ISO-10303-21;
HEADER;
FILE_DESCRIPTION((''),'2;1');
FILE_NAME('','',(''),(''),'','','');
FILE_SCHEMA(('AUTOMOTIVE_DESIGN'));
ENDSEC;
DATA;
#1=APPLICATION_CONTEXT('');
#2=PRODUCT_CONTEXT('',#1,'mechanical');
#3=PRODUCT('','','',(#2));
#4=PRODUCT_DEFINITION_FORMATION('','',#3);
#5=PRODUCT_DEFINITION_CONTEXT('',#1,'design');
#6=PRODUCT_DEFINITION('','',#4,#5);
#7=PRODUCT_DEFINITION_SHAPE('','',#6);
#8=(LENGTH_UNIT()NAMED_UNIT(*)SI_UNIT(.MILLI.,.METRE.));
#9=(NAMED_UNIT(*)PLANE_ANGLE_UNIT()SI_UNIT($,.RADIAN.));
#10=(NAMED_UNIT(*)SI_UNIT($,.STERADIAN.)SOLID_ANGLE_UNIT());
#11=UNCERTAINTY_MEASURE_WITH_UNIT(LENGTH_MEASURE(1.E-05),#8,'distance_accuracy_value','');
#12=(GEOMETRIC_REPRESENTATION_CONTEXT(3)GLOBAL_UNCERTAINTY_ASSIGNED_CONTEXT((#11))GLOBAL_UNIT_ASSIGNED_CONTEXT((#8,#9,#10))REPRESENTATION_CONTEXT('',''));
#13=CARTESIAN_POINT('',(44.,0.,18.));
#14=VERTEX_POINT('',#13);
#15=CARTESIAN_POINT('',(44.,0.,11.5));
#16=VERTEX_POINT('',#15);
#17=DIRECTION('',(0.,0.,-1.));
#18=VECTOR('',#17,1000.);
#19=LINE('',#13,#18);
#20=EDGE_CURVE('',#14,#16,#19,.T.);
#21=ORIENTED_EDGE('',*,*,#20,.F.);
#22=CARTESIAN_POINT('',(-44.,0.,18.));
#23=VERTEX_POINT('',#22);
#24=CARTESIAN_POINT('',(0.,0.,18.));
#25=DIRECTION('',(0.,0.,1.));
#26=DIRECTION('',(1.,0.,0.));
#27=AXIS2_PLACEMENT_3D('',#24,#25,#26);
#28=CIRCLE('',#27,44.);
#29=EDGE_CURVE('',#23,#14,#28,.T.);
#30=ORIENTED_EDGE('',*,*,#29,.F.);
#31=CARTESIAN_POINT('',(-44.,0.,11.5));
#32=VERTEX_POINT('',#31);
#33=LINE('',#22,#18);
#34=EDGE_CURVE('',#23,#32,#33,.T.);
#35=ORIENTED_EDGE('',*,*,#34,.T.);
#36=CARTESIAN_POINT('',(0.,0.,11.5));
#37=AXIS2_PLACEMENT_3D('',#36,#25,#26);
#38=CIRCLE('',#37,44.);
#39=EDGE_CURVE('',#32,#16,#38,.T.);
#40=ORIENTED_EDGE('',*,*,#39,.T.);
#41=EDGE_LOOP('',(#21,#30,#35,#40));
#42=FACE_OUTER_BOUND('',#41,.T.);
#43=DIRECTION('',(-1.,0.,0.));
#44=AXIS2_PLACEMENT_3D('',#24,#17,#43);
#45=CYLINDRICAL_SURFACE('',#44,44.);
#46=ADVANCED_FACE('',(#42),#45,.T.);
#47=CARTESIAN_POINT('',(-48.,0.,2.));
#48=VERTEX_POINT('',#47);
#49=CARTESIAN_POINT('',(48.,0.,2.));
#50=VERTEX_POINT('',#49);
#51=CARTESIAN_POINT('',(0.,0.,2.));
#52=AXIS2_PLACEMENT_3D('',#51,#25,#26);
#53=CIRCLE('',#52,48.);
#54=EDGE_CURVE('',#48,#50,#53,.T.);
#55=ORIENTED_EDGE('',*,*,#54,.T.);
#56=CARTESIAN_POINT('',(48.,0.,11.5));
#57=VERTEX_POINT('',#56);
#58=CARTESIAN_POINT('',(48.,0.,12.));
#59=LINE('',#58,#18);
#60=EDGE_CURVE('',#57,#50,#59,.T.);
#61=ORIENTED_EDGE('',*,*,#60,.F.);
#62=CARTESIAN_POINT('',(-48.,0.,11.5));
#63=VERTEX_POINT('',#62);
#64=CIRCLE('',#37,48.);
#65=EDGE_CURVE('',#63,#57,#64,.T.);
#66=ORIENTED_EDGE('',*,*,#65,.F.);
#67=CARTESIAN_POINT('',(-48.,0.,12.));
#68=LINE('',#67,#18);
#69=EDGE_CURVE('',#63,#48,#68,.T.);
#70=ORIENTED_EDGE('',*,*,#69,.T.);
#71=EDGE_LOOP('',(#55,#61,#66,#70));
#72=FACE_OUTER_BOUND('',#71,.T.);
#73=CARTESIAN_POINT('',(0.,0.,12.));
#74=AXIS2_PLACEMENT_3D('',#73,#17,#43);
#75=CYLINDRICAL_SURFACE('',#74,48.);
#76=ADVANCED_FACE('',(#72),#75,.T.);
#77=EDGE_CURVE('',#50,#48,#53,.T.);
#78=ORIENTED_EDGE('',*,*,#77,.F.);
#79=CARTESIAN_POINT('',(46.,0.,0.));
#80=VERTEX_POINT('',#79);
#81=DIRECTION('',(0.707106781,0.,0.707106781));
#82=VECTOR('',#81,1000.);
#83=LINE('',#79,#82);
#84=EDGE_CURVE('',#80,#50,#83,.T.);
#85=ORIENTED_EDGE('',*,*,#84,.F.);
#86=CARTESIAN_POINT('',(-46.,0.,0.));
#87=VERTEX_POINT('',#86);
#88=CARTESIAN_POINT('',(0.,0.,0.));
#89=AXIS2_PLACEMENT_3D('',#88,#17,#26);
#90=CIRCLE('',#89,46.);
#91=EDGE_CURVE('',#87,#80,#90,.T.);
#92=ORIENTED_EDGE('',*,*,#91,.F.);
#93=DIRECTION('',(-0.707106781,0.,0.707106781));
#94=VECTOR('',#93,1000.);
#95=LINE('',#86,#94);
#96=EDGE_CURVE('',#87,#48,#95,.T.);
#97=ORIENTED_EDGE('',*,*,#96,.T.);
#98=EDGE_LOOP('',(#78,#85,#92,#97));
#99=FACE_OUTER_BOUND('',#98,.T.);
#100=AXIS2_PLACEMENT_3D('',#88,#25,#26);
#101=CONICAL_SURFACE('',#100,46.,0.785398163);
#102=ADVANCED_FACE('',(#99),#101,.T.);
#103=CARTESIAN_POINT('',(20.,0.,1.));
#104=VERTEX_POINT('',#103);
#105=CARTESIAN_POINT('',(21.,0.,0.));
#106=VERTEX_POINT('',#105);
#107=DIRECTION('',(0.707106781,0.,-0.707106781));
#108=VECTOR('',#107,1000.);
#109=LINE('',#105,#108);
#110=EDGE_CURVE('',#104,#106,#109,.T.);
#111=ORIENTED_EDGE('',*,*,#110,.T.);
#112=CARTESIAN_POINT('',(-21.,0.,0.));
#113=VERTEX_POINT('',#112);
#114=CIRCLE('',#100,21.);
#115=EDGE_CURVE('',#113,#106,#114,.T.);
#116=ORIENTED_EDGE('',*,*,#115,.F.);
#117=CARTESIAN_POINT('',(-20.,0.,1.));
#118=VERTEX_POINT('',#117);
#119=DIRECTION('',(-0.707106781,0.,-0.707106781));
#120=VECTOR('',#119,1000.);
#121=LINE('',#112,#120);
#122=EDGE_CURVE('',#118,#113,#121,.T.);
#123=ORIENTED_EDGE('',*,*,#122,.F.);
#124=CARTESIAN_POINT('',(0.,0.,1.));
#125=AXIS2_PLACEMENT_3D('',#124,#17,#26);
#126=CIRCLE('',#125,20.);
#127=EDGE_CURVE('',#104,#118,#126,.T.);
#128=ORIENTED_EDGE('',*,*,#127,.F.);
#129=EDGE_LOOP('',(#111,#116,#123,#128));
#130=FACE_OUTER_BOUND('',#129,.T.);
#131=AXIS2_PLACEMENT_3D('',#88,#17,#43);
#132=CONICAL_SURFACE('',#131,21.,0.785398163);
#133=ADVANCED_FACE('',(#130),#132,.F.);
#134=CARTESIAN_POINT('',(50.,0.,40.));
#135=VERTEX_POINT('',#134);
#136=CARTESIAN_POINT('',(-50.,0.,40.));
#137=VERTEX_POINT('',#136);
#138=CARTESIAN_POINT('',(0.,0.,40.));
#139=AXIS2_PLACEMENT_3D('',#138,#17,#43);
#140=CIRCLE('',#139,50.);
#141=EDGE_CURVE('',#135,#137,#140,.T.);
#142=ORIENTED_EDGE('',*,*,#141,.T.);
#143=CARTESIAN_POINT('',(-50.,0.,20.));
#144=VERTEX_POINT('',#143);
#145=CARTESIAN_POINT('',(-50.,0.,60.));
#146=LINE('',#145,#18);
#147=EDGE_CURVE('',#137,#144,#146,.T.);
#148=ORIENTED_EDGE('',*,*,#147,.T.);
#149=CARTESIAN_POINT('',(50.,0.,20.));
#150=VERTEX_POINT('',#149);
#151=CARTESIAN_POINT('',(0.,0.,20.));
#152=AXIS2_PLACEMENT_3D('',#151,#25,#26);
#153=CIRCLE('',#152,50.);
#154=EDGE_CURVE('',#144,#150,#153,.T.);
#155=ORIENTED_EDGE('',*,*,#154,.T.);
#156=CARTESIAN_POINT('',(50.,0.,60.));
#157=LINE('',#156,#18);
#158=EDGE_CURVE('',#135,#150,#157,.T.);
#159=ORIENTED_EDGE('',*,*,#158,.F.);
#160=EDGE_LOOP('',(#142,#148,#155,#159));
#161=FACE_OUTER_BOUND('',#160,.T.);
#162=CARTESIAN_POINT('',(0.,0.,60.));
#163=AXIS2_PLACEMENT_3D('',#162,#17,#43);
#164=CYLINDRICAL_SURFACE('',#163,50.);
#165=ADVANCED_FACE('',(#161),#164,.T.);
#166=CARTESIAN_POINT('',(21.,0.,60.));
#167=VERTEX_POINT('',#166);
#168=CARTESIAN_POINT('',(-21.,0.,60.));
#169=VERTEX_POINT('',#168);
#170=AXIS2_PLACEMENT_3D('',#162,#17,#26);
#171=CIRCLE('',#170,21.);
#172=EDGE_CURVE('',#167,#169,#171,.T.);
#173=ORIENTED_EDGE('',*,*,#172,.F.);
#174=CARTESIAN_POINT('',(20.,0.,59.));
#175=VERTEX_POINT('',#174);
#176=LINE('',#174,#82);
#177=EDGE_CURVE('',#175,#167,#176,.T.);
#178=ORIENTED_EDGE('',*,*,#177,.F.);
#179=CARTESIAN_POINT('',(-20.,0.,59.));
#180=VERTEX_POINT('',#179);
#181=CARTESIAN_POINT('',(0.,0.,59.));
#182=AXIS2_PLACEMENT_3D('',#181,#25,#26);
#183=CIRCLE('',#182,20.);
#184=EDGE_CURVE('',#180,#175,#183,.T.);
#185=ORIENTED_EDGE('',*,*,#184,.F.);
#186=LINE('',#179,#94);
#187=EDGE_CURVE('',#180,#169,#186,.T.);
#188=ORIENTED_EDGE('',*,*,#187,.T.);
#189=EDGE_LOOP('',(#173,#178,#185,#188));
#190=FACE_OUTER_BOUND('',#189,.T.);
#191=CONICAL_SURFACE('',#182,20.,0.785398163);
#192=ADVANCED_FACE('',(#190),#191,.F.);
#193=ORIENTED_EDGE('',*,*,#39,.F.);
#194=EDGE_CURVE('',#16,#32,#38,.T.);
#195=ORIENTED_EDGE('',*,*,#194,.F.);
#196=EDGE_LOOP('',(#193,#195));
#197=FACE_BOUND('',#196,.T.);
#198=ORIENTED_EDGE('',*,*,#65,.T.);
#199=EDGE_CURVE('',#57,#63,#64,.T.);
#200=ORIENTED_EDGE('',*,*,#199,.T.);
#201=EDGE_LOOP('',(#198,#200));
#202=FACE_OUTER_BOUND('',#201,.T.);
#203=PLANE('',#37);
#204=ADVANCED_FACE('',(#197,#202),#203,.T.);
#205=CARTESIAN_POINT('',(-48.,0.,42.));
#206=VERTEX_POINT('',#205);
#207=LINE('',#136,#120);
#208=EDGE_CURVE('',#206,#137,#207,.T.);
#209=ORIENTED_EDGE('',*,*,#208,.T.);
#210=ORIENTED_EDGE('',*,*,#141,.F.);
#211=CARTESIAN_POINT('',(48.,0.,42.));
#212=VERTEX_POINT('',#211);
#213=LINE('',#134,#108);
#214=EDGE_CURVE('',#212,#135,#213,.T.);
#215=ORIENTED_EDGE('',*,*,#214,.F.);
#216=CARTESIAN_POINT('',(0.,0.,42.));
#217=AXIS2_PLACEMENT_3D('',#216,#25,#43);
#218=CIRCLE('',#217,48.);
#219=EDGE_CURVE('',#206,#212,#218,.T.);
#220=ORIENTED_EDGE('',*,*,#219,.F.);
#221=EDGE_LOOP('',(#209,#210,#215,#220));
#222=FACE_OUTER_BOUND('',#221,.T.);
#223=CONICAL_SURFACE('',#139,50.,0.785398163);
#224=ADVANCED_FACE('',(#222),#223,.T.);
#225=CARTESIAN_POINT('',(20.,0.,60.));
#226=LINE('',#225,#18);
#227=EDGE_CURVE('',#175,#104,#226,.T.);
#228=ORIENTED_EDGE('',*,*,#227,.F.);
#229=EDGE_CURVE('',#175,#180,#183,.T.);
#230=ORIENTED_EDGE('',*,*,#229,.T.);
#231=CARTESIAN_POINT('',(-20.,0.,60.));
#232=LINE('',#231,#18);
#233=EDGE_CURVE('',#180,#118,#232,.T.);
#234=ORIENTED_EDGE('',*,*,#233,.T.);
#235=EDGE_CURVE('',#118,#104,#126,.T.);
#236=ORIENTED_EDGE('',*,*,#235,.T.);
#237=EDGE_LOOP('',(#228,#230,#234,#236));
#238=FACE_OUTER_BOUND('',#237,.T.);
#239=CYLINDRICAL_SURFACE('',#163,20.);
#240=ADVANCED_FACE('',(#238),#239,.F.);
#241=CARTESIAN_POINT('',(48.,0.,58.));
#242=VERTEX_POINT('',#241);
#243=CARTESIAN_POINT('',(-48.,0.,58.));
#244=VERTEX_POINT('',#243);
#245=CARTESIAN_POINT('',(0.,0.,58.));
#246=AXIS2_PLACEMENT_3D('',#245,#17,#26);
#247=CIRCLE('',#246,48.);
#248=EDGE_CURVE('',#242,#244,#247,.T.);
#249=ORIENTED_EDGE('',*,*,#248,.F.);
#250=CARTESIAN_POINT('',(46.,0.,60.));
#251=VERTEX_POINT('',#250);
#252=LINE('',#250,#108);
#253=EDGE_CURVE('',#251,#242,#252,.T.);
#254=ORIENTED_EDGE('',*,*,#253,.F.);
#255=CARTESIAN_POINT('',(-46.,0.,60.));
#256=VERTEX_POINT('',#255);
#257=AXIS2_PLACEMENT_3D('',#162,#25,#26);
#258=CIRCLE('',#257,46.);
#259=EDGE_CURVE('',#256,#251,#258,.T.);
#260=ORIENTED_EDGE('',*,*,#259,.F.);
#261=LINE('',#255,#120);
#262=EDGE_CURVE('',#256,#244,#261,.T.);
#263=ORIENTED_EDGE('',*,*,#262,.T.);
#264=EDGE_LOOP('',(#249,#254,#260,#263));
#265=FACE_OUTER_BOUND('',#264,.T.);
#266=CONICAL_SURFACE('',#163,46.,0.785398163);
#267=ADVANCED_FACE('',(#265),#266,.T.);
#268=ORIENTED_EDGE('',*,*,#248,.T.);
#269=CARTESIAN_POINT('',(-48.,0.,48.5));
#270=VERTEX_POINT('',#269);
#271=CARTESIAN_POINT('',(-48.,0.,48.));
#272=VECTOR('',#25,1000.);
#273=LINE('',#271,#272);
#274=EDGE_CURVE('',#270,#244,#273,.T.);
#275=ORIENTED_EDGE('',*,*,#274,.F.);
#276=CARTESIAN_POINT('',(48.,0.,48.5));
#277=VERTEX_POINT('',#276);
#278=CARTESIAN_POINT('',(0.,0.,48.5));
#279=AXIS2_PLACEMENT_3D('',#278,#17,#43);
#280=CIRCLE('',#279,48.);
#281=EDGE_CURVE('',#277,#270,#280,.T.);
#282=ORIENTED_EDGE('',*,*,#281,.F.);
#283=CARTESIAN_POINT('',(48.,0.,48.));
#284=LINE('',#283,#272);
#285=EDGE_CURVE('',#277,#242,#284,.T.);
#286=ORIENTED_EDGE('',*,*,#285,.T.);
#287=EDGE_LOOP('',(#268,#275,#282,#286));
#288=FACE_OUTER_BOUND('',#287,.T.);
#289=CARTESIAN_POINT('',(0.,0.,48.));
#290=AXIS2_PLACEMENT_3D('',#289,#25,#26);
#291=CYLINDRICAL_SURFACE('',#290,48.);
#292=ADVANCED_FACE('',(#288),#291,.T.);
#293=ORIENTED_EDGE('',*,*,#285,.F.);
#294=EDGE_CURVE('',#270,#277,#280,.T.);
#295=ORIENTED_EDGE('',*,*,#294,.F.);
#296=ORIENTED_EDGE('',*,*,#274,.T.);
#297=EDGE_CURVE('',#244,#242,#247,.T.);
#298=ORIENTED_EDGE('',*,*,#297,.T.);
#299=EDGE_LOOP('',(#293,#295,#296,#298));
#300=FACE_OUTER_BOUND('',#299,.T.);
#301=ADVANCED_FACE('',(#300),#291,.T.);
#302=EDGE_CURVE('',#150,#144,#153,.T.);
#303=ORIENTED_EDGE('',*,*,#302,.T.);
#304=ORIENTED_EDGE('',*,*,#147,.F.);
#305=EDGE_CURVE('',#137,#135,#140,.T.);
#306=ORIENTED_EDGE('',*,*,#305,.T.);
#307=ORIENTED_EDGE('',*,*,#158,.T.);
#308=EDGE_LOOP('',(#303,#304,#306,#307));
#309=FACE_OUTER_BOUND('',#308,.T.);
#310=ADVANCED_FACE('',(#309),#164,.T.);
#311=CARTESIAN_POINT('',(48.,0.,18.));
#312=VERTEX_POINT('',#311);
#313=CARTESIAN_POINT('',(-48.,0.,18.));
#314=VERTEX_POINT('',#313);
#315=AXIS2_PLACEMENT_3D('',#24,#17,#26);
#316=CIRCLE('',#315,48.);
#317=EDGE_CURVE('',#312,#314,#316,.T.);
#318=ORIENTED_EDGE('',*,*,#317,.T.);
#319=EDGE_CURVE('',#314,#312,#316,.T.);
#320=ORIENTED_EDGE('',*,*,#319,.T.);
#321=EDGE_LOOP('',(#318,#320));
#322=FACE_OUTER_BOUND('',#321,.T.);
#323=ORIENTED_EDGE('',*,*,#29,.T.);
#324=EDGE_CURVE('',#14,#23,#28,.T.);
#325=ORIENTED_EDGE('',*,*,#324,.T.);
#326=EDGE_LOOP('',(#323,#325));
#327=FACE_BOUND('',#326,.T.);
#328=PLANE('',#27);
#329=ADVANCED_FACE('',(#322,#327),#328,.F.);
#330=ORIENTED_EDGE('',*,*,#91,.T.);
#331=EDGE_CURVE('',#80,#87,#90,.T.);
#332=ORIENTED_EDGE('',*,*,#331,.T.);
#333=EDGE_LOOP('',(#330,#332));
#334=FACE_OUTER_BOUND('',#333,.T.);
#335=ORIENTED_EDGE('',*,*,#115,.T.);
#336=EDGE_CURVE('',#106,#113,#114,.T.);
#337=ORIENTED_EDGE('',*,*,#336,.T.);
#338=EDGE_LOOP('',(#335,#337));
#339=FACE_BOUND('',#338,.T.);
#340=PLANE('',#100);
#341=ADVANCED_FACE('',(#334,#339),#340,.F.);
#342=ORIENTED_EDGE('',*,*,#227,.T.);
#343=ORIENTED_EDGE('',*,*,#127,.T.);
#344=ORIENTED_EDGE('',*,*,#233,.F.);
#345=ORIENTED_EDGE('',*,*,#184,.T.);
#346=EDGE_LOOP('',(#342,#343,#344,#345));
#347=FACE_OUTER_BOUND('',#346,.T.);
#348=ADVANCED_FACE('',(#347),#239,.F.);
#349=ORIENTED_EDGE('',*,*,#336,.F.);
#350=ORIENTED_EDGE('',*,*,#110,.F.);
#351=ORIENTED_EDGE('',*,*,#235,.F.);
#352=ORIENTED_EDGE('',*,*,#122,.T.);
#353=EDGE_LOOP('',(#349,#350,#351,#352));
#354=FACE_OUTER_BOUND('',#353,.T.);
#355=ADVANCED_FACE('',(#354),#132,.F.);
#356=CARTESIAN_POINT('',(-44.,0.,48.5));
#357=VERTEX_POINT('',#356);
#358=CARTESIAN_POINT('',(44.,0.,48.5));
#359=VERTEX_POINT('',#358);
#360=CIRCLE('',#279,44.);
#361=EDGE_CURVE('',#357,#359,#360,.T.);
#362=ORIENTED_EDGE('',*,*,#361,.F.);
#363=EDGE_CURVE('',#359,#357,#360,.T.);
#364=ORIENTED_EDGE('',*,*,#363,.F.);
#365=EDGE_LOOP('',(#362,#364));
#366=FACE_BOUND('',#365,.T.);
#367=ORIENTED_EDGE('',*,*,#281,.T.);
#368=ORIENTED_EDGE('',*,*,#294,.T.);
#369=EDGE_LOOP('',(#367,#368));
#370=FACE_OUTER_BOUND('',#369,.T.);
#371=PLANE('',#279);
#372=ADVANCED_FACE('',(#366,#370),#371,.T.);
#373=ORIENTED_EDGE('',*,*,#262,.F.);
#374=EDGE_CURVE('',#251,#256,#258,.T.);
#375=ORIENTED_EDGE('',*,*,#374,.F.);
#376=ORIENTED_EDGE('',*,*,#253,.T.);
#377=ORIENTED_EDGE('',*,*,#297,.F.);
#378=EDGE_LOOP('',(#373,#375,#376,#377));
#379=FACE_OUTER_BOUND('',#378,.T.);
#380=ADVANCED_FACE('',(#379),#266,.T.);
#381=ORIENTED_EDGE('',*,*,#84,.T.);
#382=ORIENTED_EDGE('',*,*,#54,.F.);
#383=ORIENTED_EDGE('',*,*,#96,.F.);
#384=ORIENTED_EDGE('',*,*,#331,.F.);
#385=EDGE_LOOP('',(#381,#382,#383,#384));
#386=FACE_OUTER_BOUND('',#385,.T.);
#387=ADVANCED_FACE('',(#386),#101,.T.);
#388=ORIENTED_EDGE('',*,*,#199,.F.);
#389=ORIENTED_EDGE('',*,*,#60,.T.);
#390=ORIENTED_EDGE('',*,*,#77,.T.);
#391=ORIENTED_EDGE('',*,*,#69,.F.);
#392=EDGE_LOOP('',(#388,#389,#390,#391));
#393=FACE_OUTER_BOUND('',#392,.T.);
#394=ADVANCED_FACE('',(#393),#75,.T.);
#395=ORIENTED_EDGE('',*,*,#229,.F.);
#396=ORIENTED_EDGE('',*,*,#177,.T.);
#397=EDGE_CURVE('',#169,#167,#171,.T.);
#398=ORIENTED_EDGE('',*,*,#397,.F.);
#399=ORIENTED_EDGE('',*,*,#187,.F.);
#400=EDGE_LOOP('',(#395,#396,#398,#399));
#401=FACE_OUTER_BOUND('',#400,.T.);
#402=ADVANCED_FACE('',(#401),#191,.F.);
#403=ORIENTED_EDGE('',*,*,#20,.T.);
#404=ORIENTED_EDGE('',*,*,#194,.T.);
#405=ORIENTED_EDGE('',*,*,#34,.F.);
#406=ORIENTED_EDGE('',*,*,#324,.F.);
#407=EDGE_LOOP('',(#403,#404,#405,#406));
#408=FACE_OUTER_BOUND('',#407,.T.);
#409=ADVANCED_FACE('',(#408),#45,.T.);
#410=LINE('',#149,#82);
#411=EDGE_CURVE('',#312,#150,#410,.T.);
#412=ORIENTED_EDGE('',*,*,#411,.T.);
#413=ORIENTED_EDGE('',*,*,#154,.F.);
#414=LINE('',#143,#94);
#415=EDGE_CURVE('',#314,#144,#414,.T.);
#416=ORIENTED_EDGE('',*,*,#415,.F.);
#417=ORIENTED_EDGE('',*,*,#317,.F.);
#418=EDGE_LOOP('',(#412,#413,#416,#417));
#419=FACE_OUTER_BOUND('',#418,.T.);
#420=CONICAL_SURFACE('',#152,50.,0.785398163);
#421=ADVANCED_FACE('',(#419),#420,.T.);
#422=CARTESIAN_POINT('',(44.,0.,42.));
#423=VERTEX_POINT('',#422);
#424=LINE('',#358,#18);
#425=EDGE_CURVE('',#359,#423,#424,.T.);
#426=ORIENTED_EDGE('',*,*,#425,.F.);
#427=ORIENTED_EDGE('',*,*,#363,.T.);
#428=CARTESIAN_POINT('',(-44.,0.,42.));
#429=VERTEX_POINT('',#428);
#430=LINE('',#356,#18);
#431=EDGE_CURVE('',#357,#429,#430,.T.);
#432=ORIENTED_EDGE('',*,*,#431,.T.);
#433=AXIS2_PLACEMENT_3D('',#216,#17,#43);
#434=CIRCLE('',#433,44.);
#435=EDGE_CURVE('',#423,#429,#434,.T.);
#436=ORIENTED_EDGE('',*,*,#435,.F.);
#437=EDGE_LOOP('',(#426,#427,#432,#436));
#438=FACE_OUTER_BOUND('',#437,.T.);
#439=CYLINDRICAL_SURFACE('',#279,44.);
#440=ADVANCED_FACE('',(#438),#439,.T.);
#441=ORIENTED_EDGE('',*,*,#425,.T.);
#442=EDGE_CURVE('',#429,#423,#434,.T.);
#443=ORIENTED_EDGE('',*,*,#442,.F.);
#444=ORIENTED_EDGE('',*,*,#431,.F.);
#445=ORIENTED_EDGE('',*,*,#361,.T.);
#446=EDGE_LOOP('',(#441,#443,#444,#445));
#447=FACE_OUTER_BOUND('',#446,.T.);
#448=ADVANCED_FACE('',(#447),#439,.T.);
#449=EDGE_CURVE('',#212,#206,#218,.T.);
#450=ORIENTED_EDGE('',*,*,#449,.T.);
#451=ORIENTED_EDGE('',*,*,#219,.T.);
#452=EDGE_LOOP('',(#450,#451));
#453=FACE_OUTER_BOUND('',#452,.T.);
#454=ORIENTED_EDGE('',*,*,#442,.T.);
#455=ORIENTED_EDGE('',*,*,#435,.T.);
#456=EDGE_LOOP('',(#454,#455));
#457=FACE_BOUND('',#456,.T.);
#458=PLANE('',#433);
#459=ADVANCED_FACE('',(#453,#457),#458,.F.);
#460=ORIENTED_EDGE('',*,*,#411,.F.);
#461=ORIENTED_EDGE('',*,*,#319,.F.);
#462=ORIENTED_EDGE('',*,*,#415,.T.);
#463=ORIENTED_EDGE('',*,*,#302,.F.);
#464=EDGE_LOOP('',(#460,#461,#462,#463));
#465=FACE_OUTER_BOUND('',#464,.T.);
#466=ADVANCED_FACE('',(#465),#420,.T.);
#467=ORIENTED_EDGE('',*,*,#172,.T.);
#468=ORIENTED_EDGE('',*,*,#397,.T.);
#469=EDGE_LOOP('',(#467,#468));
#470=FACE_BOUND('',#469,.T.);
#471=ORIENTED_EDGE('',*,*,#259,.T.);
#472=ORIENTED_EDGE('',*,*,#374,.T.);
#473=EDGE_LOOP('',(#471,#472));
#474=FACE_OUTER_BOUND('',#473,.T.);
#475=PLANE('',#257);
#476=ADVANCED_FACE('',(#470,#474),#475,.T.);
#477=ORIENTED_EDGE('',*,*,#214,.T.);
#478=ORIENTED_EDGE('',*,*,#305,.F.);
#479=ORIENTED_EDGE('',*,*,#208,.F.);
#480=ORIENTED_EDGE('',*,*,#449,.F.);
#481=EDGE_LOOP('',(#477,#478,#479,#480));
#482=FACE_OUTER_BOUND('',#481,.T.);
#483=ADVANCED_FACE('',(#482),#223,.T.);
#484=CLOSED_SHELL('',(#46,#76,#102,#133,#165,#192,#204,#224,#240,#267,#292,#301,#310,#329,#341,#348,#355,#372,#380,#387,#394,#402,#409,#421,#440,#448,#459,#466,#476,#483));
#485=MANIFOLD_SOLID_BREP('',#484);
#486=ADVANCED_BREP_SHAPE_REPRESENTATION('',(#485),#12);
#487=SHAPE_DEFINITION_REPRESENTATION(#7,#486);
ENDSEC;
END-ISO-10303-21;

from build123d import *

# Parameters (mm, degrees)
SKETCH1_R           = 50
SKETCH1_R_2         = 20
BOSS_EXTRUDE1_DEPTH = 60
CUT_EXTRUDE1_START  = -42
SKETCH2_R           = 50
SKETCH2_R_2         = 44
CUT_EXTRUDE1_DEPTH  = 6.5
CUT_EXTRUDE2_START  = 11.5
SKETCH3_R           = 50
SKETCH3_R_2         = 44
CUT_EXTRUDE2_DEPTH  = 6.5
CUT_EXTRUDE3_START  = -12
SKETCH5_R           = 50
SKETCH5_R_2         = 48
CUT_EXTRUDE3_DEPTH  = 12
SKETCH6_R           = 50
SKETCH6_R_2         = 48
CUT_EXTRUDE4_DEPTH  = 12
CHAMFER1_SIZE       = 2
CHAMFER2_SIZE       = 1
CHAMFER3_SIZE       = 2


with BuildPart() as part:
    # Sketch1 → Boss-Extrude1 (new body)
    with BuildSketch(Plane.XY):
        Circle(SKETCH1_R)
        Circle(SKETCH1_R_2, mode=Mode.SUBTRACT)
    extrude(amount=BOSS_EXTRUDE1_DEPTH)

    # Sketch2 → Cut-Extrude1 (cut)
    with BuildSketch(Plane(origin=(0, 0, 0), x_dir=(-1, 0, 0), z_dir=(0, 0, -1)).offset(CUT_EXTRUDE1_START)):
        Circle(SKETCH2_R)
        Circle(SKETCH2_R_2, mode=Mode.SUBTRACT)
    extrude(amount=-CUT_EXTRUDE1_DEPTH, mode=Mode.SUBTRACT)

    # Sketch3 → Cut-Extrude2 (cut)
    with BuildSketch(Plane.XY.offset(CUT_EXTRUDE2_START)):
        Circle(SKETCH3_R)
        with Locations(Location((0, 0, 0), (0, 0, 180))):
            Circle(SKETCH3_R_2, mode=Mode.SUBTRACT)
    extrude(amount=CUT_EXTRUDE2_DEPTH, mode=Mode.SUBTRACT)

    # Sketch5 → Cut-Extrude3 (cut)
    with BuildSketch(Plane.XY.offset(60).offset(CUT_EXTRUDE3_START)):
        Circle(SKETCH5_R)
        Circle(SKETCH5_R_2, mode=Mode.SUBTRACT)
    extrude(amount=CUT_EXTRUDE3_DEPTH, mode=Mode.SUBTRACT)

    # Sketch6 → Cut-Extrude4 (cut)
    with BuildSketch(Plane(origin=(0, 0, 0), x_dir=(-1, 0, 0), z_dir=(0, 0, -1))):
        Circle(SKETCH6_R)
        with Locations(Location((0, 0, 0), (0, 0, 180))):
            Circle(SKETCH6_R_2, mode=Mode.SUBTRACT)
    extrude(amount=-CUT_EXTRUDE4_DEPTH, mode=Mode.SUBTRACT)

    # Chamfer1
    chamfer1_edges = [part.edges().sort_by_distance(p)[0] for p in [
        (-48, 0, 60),
        (-48, 0, 0),
    ]]
    chamfer(chamfer1_edges, length=CHAMFER1_SIZE)

    # Chamfer2
    chamfer2_edges = [part.edges().sort_by_distance(p)[0] for p in [
        (-20, 0, 0),
        (-20, 0, 60),
    ]]
    chamfer(chamfer2_edges, length=CHAMFER2_SIZE)

    # Chamfer3
    chamfer3_edges = [part.edges().sort_by_distance(p)[0] for p in [
        (-50, 0, 42),
        (-50, 0, 18),
    ]]
    chamfer(chamfer3_edges, length=CHAMFER3_SIZE)


solid = part.part
